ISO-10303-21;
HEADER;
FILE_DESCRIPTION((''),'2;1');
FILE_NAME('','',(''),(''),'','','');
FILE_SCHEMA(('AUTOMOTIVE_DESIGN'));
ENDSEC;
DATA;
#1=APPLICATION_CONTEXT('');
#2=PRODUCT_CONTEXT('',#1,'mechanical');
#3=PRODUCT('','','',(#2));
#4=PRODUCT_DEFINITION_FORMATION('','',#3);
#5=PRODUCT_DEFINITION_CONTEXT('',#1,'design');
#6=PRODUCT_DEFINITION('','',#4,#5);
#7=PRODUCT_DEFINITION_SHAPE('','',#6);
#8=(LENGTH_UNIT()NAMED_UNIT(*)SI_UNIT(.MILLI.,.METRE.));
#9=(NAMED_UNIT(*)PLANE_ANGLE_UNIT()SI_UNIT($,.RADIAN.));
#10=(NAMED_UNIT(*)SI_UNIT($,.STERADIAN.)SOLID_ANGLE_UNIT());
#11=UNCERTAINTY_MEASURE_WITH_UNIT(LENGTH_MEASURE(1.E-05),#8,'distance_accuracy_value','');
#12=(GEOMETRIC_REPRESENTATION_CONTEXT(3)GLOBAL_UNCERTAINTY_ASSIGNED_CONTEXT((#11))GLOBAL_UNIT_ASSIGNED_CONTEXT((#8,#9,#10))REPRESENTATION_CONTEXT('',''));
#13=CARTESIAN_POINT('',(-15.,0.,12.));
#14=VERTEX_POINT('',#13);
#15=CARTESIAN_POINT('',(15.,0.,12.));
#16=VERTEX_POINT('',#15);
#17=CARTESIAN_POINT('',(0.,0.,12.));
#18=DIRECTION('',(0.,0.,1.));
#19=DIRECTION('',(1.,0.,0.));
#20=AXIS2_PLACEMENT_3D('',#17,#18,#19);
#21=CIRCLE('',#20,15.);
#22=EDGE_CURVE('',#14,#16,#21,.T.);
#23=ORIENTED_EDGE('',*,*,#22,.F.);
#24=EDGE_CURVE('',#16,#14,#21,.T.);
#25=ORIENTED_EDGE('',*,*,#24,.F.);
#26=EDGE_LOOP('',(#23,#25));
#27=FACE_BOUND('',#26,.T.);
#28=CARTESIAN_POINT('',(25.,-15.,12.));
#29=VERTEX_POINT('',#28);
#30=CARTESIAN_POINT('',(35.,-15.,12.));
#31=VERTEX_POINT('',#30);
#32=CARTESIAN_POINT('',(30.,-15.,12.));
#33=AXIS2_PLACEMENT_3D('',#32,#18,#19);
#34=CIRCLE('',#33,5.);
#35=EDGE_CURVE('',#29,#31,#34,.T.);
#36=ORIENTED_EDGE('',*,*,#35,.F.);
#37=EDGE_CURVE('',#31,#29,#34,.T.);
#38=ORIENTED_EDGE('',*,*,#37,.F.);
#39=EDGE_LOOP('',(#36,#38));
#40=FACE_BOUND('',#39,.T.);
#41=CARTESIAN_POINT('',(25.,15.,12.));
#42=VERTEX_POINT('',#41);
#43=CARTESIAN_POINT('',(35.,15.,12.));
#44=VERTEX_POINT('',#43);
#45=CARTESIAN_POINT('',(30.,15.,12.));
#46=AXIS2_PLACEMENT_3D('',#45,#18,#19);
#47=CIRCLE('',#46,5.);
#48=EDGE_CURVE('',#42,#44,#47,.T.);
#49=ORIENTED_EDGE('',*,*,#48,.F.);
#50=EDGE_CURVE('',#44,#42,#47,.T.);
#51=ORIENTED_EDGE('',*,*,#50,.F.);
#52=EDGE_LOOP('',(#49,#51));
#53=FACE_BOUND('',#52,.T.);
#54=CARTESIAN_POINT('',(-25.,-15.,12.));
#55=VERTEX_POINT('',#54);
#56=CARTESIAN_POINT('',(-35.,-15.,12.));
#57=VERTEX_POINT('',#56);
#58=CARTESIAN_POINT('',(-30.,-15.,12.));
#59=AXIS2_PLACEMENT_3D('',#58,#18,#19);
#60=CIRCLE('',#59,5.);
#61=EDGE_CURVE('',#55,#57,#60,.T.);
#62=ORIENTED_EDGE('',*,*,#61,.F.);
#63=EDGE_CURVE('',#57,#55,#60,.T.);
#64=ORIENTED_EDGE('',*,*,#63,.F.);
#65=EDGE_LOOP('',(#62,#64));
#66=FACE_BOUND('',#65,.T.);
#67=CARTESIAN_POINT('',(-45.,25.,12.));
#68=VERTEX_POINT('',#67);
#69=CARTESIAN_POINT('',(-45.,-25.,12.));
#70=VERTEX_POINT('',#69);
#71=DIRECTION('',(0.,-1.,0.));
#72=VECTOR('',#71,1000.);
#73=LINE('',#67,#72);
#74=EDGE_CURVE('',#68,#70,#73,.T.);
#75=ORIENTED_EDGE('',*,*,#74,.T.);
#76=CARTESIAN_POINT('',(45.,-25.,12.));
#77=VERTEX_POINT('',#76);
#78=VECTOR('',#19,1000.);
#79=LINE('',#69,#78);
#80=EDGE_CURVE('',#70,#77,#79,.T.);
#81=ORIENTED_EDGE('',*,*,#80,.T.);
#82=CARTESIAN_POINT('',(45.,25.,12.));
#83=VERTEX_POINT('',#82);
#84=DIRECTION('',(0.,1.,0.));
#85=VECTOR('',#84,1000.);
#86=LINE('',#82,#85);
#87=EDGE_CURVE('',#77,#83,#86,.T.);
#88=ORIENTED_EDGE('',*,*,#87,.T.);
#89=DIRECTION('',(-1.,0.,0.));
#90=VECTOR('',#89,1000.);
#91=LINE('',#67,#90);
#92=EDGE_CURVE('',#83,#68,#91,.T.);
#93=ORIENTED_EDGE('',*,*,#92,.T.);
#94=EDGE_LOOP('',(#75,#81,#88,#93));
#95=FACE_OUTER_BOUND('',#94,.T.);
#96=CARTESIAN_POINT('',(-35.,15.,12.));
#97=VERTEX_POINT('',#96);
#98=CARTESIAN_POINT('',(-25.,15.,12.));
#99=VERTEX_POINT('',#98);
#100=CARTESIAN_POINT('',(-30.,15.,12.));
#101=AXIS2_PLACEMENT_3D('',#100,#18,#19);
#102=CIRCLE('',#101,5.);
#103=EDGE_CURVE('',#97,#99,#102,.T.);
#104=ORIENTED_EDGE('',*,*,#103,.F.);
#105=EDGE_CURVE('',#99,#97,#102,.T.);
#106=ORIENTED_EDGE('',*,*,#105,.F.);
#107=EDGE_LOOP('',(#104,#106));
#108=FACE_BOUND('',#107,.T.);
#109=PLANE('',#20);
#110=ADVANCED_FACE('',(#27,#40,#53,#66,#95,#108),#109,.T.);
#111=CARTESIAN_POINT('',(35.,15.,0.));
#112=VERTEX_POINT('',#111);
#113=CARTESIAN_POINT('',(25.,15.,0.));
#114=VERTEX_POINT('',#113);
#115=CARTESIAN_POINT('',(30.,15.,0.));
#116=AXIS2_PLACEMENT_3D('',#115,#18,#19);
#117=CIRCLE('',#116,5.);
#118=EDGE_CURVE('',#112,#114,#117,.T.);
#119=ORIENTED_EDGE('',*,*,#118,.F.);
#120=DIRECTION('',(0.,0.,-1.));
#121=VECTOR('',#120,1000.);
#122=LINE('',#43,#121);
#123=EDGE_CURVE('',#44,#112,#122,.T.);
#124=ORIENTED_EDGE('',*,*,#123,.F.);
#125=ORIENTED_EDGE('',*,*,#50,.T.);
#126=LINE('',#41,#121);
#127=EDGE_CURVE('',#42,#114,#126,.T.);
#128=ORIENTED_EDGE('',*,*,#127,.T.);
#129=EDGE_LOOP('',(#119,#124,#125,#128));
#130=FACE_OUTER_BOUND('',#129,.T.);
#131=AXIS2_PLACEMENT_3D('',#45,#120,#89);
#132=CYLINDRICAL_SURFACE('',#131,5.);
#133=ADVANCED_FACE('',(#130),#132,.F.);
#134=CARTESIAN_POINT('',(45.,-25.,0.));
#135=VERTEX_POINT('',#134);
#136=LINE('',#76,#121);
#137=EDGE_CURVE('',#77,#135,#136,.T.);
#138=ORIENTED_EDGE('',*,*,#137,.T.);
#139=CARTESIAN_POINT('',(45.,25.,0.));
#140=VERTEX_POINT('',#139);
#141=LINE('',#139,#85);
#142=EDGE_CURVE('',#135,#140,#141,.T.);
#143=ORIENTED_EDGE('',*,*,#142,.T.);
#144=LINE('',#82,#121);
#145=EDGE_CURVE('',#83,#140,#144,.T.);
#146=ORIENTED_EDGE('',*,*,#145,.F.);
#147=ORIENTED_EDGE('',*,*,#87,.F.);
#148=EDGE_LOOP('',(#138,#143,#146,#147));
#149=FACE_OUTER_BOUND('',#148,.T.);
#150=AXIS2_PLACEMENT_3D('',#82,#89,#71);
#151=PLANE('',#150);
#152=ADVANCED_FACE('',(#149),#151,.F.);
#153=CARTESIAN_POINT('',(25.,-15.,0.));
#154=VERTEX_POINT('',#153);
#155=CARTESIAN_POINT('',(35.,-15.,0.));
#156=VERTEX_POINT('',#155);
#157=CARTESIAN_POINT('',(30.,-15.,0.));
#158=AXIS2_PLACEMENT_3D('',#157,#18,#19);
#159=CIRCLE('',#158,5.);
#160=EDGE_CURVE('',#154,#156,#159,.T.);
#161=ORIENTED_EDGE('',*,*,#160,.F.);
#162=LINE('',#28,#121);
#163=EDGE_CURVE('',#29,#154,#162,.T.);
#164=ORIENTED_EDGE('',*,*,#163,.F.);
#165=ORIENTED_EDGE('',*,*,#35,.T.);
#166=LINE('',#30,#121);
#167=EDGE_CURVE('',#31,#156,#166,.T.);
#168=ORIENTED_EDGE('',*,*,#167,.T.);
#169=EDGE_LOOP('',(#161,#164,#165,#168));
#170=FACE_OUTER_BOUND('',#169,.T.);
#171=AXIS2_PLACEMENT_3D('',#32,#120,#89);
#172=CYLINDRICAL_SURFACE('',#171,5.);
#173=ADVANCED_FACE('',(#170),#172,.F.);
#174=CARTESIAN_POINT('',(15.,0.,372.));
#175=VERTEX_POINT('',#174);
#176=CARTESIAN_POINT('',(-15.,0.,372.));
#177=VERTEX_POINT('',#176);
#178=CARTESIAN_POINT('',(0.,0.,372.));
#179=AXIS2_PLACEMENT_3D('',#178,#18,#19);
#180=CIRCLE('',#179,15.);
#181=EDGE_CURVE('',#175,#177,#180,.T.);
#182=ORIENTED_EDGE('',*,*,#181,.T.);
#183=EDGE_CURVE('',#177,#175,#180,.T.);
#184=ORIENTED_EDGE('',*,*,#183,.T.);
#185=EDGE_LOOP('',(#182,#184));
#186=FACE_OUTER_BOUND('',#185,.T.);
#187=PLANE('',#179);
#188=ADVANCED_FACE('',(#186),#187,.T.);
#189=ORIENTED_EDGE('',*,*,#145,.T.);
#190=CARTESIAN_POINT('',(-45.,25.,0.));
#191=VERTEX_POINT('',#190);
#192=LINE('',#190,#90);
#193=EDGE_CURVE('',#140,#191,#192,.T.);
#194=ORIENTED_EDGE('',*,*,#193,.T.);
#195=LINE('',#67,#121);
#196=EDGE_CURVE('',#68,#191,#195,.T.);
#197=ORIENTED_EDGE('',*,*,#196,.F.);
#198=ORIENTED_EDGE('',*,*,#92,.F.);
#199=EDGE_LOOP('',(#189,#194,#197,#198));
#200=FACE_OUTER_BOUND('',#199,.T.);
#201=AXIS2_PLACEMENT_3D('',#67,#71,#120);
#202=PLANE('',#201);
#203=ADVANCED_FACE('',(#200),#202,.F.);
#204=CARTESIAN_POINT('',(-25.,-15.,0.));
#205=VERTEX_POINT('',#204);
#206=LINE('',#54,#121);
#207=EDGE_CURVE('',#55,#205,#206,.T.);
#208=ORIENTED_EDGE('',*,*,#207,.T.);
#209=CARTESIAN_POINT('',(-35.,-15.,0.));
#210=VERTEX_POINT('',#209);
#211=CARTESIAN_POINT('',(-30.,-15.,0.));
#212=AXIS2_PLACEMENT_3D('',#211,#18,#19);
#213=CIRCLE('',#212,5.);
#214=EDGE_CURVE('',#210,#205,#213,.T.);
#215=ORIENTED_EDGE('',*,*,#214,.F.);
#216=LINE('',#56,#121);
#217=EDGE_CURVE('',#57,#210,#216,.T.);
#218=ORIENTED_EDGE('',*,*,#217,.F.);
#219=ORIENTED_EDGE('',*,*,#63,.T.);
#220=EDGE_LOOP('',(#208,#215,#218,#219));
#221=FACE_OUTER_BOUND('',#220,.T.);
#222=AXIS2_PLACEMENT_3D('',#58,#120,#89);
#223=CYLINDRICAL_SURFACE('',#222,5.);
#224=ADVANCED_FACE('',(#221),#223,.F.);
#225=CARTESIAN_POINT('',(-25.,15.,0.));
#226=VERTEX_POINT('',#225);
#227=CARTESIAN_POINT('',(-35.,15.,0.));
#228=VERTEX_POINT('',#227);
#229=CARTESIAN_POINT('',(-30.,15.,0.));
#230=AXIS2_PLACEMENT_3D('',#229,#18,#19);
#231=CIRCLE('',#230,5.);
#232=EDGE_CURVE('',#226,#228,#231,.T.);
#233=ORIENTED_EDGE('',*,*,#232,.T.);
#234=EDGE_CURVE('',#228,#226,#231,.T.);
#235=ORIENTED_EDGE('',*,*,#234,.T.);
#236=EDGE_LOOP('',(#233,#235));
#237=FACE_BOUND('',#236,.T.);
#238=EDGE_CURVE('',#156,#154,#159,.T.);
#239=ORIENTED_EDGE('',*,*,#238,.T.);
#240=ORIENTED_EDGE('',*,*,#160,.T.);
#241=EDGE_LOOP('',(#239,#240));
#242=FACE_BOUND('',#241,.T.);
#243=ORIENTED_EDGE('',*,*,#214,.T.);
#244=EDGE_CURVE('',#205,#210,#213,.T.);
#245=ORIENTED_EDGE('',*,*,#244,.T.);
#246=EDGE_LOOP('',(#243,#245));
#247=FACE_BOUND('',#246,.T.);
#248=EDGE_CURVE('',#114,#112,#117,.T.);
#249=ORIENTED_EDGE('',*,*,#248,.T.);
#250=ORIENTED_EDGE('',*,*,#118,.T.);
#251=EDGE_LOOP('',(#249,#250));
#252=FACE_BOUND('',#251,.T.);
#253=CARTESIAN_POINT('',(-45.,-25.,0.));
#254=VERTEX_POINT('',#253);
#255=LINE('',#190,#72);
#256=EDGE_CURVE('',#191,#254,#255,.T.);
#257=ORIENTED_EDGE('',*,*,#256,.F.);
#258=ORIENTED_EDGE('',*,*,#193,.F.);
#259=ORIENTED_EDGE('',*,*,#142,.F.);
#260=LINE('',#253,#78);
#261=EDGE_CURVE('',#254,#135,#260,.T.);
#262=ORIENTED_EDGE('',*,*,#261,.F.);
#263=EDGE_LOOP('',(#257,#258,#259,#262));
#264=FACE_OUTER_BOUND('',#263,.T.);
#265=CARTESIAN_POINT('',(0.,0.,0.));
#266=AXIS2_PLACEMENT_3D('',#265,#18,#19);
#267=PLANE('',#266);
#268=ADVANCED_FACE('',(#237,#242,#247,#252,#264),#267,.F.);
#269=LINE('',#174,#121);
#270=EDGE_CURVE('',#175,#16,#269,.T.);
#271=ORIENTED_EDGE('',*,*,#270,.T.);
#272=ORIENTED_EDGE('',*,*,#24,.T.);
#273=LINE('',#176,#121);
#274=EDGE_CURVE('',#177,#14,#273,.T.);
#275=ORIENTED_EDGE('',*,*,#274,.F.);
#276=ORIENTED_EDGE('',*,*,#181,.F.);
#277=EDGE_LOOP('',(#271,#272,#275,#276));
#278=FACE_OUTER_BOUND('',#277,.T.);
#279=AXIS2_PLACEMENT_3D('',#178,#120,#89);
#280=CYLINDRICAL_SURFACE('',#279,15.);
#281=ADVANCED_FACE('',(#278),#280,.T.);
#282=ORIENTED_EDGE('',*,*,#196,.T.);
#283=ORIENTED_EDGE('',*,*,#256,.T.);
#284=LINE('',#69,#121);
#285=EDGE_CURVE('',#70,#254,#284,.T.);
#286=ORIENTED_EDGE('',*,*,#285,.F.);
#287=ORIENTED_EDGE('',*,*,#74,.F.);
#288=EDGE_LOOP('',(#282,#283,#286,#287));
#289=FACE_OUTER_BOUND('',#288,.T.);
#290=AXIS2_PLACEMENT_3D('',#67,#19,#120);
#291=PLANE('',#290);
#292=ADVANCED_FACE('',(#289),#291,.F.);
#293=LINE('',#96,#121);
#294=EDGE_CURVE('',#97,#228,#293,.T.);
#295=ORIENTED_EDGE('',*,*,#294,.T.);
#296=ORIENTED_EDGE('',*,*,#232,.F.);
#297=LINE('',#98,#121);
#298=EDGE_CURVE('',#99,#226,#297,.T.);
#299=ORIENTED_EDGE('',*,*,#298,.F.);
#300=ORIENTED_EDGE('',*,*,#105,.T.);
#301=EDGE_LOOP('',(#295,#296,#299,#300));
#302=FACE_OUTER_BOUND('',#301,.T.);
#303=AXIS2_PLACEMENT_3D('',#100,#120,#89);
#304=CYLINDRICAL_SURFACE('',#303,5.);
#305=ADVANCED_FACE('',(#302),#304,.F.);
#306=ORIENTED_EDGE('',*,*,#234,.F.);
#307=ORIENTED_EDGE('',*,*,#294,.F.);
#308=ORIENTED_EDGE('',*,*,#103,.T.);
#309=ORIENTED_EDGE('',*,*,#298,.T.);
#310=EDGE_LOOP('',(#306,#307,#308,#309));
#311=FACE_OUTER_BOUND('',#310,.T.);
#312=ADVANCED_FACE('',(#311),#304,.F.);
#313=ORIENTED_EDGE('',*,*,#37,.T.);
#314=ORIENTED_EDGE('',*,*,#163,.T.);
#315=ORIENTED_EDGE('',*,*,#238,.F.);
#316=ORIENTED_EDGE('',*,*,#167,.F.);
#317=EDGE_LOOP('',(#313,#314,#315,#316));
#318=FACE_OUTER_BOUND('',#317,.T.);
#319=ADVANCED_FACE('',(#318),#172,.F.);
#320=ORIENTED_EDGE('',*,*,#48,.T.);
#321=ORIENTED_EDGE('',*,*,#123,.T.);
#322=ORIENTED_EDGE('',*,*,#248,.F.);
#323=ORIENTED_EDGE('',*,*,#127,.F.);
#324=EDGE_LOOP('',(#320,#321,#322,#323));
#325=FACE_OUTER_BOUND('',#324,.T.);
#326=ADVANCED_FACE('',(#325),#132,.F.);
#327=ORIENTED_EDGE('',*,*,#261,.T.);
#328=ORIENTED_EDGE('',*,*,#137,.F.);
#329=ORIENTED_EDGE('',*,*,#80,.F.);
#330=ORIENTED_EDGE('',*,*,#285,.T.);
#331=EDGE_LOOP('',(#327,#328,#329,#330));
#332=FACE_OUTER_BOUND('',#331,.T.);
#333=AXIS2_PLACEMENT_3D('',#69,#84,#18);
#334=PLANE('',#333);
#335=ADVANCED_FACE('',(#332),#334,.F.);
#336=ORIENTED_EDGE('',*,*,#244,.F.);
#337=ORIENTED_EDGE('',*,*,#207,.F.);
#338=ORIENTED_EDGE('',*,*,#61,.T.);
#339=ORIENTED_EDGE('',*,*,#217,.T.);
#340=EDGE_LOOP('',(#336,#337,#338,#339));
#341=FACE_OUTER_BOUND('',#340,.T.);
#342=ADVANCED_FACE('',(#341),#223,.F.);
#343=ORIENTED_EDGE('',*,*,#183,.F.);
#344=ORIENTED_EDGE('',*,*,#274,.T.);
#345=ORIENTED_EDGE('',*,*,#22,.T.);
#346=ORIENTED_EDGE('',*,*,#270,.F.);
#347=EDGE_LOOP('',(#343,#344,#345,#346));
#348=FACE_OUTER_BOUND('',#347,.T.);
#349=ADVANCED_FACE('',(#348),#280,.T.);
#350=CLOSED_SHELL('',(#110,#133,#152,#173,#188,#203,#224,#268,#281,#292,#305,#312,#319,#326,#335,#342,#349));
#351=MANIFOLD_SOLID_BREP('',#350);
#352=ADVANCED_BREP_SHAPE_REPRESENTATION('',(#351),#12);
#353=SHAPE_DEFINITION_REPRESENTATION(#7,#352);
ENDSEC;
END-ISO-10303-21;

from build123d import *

# Parameters (mm, degrees)
SKETCH1_W           = 90
SKETCH1_H           = 50
SKETCH1_R           = 5
BOSS_EXTRUDE1_DEPTH = 12
SKETCH2_R           = 15
BOSS_EXTRUDE2_DEPTH = 360


with BuildPart() as part:
    # Sketch1 → Boss-Extrude1 (new body)
    with BuildSketch(Plane.XY):
        Rectangle(SKETCH1_W, SKETCH1_H)
        with Locations((-30, 15)):
            Circle(SKETCH1_R, mode=Mode.SUBTRACT)
        with Locations((-30, -15)):
            Circle(SKETCH1_R, mode=Mode.SUBTRACT)
        with Locations((30, -15)):
            Circle(SKETCH1_R, mode=Mode.SUBTRACT)
        with Locations((30, 15)):
            Circle(SKETCH1_R, mode=Mode.SUBTRACT)
    extrude(amount=BOSS_EXTRUDE1_DEPTH)

    # Sketch2 → Boss-Extrude2 (add)
    with BuildSketch(Plane.XY.offset(12)):
        with Locations(Location((0, 0, 0), (0, 0, 180))):
            Circle(SKETCH2_R)
    extrude(amount=BOSS_EXTRUDE2_DEPTH)


solid = part.part
